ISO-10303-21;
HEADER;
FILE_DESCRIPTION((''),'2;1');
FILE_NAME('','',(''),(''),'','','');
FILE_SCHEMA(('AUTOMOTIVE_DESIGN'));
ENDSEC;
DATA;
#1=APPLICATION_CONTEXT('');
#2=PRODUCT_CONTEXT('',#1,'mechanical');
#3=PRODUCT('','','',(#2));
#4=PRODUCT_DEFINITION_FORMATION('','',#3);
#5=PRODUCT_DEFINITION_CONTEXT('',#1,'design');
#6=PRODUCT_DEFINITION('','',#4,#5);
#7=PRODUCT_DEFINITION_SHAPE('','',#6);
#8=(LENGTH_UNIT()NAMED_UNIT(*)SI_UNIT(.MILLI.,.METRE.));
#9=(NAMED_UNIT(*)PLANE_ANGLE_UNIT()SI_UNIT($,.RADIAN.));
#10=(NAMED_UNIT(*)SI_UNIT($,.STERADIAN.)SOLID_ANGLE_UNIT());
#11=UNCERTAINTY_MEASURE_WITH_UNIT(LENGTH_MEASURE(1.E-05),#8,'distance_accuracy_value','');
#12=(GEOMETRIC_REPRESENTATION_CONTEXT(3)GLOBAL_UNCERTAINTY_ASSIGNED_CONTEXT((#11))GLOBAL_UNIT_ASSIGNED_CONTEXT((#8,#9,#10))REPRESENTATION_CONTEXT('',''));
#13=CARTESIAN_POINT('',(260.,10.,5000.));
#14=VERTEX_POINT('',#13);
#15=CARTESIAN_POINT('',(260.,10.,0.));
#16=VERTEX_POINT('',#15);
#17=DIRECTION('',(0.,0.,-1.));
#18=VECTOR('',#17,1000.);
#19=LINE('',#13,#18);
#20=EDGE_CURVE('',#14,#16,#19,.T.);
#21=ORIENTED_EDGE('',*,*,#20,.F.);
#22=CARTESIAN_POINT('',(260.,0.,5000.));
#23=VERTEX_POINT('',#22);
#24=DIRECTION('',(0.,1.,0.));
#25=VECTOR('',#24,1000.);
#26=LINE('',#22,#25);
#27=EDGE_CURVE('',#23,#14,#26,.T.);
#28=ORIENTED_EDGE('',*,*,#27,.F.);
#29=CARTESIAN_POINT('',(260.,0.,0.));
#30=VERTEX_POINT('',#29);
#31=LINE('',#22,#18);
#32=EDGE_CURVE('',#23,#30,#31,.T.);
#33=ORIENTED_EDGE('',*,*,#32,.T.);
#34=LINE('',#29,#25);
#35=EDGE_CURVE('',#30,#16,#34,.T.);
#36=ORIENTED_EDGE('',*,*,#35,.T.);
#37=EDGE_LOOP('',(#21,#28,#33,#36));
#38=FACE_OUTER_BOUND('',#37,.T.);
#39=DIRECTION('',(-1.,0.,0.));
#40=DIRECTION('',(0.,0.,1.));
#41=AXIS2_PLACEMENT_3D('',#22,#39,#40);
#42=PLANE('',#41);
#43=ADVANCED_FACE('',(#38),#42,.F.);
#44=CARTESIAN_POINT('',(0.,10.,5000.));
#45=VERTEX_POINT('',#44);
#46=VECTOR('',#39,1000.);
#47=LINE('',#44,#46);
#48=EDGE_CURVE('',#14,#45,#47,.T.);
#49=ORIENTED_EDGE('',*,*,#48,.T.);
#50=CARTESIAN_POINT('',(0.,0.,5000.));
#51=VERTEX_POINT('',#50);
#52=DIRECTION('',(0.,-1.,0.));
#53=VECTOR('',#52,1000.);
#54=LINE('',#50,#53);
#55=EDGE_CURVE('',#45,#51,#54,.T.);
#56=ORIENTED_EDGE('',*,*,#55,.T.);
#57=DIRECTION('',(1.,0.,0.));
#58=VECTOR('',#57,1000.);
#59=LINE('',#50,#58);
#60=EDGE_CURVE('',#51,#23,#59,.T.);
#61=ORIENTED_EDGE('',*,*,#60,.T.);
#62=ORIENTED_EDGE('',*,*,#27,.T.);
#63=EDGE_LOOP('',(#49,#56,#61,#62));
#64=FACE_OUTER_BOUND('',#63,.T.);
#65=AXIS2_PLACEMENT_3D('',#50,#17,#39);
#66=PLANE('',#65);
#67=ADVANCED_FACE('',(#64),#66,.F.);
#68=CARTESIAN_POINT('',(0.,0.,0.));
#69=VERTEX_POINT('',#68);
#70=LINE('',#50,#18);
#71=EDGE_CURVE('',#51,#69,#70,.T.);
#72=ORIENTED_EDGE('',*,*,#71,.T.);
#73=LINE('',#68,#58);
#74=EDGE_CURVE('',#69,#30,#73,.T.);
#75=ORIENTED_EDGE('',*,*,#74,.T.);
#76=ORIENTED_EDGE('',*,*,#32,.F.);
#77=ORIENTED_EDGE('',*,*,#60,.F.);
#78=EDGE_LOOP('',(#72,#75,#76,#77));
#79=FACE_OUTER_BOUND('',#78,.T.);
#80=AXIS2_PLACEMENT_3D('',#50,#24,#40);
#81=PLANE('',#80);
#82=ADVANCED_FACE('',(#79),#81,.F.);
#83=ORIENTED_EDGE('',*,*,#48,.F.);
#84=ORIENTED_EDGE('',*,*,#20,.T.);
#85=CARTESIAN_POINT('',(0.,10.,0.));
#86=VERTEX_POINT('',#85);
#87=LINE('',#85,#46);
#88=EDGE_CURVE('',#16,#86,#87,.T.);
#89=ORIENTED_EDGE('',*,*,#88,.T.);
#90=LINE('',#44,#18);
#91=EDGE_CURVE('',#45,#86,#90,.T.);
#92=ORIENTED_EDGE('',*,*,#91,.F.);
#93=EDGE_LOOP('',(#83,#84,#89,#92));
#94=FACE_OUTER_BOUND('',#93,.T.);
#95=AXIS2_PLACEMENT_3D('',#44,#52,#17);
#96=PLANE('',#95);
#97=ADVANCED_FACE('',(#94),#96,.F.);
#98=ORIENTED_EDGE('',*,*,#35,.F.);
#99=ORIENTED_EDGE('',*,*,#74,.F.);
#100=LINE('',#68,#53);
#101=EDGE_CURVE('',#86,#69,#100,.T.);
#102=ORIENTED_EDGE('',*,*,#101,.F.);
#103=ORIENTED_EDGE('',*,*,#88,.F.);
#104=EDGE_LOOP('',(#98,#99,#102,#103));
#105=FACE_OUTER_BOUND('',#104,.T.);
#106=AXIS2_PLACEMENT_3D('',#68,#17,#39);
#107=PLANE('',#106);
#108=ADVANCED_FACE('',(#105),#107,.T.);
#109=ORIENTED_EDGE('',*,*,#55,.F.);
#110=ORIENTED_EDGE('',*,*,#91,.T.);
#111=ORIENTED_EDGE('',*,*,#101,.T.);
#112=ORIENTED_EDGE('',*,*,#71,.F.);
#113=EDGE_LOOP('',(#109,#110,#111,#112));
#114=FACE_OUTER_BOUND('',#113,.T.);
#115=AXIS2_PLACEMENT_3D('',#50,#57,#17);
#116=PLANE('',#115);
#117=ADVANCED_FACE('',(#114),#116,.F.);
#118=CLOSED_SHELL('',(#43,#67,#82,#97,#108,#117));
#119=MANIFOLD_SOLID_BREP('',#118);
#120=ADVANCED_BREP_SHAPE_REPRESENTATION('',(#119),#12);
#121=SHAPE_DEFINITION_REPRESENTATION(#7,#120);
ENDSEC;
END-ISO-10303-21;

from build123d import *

# Parameters (mm, degrees)
SKETCH1_W           = 260
SKETCH1_H           = 10
BOSS_EXTRUDE1_DEPTH = 5000


with BuildPart() as part:
    # Sketch1 → Boss-Extrude1 (new body)
    with BuildSketch(Plane.XY):
        with Locations((130, 5)):
            Rectangle(SKETCH1_W, SKETCH1_H)
    extrude(amount=BOSS_EXTRUDE1_DEPTH)


solid = part.part
